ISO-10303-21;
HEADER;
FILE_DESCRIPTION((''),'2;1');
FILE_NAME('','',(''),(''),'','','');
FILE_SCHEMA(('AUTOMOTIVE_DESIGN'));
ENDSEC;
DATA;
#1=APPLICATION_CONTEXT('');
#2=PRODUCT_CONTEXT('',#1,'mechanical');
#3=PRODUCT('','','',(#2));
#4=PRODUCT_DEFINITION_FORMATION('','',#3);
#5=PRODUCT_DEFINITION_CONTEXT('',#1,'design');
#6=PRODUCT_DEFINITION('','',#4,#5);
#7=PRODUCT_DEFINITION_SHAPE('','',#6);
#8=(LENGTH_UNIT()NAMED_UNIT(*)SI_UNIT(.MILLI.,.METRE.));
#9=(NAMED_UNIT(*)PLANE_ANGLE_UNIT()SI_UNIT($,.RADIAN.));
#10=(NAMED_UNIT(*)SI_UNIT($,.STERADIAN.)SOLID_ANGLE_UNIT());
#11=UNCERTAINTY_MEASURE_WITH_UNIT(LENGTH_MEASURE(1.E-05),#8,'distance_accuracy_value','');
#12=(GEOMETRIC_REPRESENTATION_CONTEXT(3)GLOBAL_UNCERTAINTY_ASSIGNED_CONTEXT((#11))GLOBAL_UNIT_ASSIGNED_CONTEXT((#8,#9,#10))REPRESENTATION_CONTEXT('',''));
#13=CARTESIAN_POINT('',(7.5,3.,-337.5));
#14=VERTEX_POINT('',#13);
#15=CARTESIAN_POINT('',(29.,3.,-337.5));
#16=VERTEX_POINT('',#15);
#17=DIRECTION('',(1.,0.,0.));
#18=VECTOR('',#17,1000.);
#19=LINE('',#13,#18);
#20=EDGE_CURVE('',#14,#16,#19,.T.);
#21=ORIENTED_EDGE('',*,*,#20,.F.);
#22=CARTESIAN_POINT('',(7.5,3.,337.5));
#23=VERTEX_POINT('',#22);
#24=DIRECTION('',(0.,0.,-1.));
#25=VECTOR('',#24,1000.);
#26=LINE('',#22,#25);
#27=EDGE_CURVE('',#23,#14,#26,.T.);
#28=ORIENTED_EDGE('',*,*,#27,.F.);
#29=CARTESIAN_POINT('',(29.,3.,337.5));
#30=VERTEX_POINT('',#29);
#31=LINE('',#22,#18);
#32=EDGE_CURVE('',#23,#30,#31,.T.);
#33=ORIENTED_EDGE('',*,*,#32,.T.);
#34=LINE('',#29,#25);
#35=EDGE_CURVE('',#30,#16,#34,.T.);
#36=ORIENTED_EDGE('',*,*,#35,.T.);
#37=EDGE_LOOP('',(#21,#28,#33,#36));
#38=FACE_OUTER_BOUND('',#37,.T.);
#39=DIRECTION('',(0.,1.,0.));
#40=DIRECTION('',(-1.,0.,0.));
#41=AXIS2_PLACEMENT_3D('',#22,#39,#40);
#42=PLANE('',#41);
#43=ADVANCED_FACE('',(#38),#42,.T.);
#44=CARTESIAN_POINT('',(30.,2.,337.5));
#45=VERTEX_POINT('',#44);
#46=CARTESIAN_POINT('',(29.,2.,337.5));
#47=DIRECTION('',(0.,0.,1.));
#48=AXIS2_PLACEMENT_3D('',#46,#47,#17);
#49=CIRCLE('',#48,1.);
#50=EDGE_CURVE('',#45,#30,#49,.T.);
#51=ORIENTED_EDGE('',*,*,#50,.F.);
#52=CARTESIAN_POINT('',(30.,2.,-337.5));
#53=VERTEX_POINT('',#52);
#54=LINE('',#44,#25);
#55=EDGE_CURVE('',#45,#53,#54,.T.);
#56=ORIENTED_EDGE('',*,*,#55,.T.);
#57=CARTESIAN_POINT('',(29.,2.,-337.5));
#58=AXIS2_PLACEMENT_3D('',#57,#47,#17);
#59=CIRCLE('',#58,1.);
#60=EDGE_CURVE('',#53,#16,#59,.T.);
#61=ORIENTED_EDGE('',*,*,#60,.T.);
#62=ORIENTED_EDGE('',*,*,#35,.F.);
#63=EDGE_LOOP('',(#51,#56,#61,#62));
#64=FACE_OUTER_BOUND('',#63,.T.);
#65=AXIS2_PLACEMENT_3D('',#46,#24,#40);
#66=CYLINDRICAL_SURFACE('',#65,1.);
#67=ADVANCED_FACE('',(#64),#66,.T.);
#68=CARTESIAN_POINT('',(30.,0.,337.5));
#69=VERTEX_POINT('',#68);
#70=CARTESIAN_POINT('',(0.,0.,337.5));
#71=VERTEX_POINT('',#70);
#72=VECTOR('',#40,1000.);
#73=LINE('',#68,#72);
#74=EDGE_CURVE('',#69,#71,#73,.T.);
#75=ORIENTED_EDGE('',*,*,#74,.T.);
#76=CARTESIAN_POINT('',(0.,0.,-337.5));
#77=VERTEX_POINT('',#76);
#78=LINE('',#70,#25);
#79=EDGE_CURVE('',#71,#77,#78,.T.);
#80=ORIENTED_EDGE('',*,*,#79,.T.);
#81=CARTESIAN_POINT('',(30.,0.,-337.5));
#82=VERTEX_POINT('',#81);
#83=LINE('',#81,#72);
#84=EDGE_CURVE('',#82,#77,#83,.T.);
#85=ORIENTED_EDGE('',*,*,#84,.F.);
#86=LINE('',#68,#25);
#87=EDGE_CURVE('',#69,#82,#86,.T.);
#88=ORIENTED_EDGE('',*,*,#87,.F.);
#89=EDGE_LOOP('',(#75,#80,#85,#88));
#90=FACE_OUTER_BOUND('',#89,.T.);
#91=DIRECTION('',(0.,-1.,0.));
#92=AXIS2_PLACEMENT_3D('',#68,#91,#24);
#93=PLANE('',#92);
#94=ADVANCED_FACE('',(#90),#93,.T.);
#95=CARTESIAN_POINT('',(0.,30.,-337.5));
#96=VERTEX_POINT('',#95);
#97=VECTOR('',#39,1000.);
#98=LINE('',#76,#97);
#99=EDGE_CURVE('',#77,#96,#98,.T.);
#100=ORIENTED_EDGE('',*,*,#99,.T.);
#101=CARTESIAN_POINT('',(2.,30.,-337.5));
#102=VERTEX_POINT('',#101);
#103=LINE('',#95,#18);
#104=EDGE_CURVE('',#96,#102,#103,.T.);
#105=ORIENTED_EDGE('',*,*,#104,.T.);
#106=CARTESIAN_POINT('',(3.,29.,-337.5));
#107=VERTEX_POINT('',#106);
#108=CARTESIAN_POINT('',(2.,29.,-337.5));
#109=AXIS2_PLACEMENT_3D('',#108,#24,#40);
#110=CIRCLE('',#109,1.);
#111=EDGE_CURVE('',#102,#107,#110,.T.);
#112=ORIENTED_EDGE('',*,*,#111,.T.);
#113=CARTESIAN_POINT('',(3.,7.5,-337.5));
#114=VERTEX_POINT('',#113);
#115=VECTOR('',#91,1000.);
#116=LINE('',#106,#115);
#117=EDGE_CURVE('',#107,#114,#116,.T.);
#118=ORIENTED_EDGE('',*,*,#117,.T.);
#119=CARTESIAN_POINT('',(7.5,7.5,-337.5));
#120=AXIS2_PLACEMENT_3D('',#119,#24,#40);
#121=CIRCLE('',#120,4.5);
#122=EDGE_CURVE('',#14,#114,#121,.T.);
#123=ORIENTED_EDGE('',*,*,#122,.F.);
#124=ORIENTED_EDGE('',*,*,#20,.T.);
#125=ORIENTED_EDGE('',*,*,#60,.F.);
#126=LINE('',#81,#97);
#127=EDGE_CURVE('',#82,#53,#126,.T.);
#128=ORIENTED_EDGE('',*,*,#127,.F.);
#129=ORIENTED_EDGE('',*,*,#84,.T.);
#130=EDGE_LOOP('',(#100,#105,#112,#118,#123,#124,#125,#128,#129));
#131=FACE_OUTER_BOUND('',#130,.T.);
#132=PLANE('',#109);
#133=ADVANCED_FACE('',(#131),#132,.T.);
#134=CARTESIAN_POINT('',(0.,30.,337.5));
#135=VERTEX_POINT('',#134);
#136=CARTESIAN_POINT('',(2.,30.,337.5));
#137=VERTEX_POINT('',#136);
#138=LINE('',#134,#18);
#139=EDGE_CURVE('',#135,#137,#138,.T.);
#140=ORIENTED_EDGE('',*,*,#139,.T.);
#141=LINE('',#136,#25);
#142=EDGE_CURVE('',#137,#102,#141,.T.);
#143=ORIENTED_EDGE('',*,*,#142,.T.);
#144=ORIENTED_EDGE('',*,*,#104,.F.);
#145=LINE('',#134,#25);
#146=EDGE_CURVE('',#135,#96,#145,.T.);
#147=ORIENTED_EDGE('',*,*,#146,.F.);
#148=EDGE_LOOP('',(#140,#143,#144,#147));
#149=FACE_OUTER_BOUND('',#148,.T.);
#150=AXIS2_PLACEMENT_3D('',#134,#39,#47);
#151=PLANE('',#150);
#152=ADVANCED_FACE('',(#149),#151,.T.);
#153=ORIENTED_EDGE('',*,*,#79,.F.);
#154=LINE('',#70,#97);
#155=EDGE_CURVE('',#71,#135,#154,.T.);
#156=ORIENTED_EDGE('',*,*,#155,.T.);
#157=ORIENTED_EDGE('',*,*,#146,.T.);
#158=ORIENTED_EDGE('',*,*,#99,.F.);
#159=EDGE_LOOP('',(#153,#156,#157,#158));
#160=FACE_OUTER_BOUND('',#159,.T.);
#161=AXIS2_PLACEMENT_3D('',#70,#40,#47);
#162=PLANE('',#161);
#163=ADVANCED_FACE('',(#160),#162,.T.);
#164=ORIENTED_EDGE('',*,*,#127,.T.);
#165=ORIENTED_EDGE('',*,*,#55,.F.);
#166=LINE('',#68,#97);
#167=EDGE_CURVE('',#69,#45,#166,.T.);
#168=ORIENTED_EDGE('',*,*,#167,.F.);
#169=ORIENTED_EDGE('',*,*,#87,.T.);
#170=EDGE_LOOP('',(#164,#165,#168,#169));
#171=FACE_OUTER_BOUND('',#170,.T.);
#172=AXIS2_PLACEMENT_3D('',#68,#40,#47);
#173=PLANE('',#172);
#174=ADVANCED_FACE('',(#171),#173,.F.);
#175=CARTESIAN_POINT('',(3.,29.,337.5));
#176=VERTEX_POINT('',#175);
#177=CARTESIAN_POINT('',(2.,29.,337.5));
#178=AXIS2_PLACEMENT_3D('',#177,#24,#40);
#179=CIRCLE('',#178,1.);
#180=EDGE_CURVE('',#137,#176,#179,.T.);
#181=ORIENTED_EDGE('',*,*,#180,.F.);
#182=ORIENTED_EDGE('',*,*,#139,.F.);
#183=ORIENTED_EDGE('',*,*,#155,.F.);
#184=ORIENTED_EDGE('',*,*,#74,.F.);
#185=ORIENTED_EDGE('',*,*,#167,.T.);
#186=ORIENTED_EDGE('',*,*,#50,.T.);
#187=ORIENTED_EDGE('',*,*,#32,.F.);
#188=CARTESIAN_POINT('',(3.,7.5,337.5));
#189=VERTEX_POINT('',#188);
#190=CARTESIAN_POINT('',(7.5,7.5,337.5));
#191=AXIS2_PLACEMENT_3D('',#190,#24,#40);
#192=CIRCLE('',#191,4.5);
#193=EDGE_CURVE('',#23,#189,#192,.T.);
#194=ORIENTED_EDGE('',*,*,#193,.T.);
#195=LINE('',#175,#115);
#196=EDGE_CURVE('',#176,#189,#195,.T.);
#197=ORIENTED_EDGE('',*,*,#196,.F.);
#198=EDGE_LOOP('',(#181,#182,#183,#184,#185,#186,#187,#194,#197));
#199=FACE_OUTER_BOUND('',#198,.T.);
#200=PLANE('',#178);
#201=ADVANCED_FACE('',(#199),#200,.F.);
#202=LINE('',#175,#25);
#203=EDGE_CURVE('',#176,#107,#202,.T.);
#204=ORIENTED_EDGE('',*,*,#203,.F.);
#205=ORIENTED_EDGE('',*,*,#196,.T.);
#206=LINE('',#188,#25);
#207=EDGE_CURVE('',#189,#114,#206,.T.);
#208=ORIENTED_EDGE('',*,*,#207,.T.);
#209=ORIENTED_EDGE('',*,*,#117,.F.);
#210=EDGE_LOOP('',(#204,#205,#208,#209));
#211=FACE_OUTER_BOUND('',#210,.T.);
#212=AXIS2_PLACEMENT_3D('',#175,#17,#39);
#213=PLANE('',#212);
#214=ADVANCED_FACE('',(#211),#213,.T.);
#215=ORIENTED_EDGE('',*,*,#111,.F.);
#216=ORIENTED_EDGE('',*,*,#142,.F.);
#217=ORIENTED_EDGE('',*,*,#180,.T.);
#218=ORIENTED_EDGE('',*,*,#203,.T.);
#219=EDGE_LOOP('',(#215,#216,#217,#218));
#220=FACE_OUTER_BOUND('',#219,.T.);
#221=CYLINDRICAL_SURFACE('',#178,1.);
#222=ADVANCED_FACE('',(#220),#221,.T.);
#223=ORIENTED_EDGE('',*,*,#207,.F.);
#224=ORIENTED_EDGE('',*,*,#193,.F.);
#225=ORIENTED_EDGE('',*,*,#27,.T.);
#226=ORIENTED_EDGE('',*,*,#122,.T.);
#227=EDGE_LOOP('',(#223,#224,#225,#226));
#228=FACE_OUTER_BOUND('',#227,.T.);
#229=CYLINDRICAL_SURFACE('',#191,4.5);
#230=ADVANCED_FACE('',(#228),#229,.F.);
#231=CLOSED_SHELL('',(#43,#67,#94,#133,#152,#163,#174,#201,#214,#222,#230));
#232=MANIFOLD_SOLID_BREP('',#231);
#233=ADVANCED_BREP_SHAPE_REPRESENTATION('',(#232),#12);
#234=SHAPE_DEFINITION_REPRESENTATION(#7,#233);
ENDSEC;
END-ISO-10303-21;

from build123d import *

# Parameters (mm, degrees)
BOSS_EXTRUDE1_DEPTH = 337.5


with BuildPart() as part:
    # Sketch1 → Boss-Extrude1 (new, symmetric)
    with BuildSketch(Plane.XY):
        with BuildLine():
            Line((0, 0), (0, 30))
            Line((0, 30), (2, 30))
            ThreePointArc((2, 30), (2.707106781, 29.707106781), (3, 29))
            Line((3, 29), (3, 7.5))
            ThreePointArc((3, 7.5), (4.318019485, 4.318019485), (7.5, 3))
            Line((7.5, 3), (29, 3))
            ThreePointArc((29, 3), (29.707106781, 2.707106781), (30, 2))
            Line((30, 2), (30, 0))
            Line((30, 0), (0, 0))
        make_face()
    extrude(amount=BOSS_EXTRUDE1_DEPTH, both=True)


solid = part.part
